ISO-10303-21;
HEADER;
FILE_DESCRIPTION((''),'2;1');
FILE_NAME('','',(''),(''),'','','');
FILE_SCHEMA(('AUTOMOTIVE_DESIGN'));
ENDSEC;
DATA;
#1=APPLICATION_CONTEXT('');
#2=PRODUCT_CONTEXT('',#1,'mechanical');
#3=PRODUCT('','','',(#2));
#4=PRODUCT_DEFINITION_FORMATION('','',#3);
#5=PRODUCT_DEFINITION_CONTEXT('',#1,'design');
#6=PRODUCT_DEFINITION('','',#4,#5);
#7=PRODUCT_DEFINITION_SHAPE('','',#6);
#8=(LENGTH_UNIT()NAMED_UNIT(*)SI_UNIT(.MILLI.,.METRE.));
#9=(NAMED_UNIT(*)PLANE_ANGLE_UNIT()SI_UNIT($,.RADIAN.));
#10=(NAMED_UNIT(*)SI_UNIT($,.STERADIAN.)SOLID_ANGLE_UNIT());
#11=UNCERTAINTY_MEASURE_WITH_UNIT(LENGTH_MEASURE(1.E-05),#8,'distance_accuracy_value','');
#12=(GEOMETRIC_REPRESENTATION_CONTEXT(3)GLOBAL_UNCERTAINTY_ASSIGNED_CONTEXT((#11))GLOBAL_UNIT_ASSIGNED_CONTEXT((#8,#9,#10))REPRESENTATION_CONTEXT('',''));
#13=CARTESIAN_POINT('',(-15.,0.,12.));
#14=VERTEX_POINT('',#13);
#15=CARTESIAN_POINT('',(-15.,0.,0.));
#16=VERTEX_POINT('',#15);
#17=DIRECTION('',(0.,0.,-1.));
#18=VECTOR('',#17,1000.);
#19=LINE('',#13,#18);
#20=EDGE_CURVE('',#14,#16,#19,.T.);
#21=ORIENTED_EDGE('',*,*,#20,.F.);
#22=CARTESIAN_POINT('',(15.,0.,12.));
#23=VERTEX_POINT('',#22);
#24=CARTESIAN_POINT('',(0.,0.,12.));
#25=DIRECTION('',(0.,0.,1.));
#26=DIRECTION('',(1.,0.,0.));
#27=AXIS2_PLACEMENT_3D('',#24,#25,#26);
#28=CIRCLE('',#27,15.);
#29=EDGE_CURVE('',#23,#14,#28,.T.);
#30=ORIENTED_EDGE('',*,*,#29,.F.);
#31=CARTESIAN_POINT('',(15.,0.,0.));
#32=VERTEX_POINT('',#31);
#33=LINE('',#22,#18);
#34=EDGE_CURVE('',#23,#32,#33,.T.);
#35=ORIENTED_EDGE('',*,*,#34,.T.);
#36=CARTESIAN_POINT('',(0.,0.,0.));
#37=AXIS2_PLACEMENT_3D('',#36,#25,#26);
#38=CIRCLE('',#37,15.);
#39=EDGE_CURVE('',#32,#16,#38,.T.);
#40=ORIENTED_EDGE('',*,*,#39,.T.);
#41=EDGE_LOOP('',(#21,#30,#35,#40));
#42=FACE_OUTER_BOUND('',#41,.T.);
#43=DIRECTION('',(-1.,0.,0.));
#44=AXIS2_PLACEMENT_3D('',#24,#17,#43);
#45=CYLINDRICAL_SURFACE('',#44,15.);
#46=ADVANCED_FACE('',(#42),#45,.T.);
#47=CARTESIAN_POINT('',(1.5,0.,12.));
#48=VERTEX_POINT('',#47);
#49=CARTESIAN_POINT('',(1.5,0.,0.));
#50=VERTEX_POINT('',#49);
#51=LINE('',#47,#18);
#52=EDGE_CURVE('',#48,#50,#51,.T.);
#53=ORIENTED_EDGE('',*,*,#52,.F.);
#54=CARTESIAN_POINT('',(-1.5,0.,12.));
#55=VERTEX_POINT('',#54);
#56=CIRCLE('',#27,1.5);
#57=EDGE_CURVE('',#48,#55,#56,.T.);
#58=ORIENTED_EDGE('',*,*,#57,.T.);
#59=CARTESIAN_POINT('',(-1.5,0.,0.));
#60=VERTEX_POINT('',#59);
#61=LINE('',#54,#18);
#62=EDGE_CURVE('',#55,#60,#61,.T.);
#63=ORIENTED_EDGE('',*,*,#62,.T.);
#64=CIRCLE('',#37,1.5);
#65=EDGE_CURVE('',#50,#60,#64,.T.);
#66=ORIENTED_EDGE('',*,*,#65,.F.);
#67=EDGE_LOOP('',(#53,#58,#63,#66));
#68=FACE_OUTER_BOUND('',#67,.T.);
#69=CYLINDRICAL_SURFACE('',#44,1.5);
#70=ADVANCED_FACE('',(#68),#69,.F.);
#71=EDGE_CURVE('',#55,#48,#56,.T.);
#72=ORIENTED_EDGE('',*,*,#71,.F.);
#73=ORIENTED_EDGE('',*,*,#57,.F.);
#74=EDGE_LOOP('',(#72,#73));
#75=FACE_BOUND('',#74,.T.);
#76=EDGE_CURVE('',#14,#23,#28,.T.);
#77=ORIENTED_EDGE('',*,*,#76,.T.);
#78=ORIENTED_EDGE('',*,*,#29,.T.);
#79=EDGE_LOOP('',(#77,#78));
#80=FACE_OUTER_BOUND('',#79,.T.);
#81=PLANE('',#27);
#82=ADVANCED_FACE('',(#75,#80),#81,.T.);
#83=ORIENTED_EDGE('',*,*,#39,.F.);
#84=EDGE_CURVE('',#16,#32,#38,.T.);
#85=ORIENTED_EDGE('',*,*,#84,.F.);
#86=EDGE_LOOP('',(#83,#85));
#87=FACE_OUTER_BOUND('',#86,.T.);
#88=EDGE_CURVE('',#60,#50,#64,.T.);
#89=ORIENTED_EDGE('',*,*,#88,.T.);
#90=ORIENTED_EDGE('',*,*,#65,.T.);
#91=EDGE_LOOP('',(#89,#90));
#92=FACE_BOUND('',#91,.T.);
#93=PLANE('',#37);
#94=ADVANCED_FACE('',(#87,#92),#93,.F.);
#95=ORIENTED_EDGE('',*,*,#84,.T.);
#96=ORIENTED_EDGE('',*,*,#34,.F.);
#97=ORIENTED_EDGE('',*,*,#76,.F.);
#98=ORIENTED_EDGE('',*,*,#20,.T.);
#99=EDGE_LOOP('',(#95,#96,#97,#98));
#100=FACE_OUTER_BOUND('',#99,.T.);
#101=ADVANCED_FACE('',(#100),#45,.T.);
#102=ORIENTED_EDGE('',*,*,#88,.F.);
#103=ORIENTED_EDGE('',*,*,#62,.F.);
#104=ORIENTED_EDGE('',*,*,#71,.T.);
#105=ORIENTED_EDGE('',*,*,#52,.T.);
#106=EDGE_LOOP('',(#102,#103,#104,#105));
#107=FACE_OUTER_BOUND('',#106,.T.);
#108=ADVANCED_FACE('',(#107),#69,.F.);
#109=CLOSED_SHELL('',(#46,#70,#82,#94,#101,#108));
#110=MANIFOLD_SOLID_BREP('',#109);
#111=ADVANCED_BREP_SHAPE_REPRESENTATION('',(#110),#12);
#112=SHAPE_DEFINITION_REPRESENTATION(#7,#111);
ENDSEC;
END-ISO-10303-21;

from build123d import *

# Parameters (mm, degrees)
SKETCH1_R           = 15
SKETCH1_R_2         = 1.5
BOSS_EXTRUDE1_DEPTH = 12


with BuildPart() as part:
    # Sketch1 → Boss-Extrude1 (new body)
    with BuildSketch(Plane.XY):
        Circle(SKETCH1_R)
        Circle(SKETCH1_R_2, mode=Mode.SUBTRACT)
    extrude(amount=BOSS_EXTRUDE1_DEPTH)


solid = part.part
